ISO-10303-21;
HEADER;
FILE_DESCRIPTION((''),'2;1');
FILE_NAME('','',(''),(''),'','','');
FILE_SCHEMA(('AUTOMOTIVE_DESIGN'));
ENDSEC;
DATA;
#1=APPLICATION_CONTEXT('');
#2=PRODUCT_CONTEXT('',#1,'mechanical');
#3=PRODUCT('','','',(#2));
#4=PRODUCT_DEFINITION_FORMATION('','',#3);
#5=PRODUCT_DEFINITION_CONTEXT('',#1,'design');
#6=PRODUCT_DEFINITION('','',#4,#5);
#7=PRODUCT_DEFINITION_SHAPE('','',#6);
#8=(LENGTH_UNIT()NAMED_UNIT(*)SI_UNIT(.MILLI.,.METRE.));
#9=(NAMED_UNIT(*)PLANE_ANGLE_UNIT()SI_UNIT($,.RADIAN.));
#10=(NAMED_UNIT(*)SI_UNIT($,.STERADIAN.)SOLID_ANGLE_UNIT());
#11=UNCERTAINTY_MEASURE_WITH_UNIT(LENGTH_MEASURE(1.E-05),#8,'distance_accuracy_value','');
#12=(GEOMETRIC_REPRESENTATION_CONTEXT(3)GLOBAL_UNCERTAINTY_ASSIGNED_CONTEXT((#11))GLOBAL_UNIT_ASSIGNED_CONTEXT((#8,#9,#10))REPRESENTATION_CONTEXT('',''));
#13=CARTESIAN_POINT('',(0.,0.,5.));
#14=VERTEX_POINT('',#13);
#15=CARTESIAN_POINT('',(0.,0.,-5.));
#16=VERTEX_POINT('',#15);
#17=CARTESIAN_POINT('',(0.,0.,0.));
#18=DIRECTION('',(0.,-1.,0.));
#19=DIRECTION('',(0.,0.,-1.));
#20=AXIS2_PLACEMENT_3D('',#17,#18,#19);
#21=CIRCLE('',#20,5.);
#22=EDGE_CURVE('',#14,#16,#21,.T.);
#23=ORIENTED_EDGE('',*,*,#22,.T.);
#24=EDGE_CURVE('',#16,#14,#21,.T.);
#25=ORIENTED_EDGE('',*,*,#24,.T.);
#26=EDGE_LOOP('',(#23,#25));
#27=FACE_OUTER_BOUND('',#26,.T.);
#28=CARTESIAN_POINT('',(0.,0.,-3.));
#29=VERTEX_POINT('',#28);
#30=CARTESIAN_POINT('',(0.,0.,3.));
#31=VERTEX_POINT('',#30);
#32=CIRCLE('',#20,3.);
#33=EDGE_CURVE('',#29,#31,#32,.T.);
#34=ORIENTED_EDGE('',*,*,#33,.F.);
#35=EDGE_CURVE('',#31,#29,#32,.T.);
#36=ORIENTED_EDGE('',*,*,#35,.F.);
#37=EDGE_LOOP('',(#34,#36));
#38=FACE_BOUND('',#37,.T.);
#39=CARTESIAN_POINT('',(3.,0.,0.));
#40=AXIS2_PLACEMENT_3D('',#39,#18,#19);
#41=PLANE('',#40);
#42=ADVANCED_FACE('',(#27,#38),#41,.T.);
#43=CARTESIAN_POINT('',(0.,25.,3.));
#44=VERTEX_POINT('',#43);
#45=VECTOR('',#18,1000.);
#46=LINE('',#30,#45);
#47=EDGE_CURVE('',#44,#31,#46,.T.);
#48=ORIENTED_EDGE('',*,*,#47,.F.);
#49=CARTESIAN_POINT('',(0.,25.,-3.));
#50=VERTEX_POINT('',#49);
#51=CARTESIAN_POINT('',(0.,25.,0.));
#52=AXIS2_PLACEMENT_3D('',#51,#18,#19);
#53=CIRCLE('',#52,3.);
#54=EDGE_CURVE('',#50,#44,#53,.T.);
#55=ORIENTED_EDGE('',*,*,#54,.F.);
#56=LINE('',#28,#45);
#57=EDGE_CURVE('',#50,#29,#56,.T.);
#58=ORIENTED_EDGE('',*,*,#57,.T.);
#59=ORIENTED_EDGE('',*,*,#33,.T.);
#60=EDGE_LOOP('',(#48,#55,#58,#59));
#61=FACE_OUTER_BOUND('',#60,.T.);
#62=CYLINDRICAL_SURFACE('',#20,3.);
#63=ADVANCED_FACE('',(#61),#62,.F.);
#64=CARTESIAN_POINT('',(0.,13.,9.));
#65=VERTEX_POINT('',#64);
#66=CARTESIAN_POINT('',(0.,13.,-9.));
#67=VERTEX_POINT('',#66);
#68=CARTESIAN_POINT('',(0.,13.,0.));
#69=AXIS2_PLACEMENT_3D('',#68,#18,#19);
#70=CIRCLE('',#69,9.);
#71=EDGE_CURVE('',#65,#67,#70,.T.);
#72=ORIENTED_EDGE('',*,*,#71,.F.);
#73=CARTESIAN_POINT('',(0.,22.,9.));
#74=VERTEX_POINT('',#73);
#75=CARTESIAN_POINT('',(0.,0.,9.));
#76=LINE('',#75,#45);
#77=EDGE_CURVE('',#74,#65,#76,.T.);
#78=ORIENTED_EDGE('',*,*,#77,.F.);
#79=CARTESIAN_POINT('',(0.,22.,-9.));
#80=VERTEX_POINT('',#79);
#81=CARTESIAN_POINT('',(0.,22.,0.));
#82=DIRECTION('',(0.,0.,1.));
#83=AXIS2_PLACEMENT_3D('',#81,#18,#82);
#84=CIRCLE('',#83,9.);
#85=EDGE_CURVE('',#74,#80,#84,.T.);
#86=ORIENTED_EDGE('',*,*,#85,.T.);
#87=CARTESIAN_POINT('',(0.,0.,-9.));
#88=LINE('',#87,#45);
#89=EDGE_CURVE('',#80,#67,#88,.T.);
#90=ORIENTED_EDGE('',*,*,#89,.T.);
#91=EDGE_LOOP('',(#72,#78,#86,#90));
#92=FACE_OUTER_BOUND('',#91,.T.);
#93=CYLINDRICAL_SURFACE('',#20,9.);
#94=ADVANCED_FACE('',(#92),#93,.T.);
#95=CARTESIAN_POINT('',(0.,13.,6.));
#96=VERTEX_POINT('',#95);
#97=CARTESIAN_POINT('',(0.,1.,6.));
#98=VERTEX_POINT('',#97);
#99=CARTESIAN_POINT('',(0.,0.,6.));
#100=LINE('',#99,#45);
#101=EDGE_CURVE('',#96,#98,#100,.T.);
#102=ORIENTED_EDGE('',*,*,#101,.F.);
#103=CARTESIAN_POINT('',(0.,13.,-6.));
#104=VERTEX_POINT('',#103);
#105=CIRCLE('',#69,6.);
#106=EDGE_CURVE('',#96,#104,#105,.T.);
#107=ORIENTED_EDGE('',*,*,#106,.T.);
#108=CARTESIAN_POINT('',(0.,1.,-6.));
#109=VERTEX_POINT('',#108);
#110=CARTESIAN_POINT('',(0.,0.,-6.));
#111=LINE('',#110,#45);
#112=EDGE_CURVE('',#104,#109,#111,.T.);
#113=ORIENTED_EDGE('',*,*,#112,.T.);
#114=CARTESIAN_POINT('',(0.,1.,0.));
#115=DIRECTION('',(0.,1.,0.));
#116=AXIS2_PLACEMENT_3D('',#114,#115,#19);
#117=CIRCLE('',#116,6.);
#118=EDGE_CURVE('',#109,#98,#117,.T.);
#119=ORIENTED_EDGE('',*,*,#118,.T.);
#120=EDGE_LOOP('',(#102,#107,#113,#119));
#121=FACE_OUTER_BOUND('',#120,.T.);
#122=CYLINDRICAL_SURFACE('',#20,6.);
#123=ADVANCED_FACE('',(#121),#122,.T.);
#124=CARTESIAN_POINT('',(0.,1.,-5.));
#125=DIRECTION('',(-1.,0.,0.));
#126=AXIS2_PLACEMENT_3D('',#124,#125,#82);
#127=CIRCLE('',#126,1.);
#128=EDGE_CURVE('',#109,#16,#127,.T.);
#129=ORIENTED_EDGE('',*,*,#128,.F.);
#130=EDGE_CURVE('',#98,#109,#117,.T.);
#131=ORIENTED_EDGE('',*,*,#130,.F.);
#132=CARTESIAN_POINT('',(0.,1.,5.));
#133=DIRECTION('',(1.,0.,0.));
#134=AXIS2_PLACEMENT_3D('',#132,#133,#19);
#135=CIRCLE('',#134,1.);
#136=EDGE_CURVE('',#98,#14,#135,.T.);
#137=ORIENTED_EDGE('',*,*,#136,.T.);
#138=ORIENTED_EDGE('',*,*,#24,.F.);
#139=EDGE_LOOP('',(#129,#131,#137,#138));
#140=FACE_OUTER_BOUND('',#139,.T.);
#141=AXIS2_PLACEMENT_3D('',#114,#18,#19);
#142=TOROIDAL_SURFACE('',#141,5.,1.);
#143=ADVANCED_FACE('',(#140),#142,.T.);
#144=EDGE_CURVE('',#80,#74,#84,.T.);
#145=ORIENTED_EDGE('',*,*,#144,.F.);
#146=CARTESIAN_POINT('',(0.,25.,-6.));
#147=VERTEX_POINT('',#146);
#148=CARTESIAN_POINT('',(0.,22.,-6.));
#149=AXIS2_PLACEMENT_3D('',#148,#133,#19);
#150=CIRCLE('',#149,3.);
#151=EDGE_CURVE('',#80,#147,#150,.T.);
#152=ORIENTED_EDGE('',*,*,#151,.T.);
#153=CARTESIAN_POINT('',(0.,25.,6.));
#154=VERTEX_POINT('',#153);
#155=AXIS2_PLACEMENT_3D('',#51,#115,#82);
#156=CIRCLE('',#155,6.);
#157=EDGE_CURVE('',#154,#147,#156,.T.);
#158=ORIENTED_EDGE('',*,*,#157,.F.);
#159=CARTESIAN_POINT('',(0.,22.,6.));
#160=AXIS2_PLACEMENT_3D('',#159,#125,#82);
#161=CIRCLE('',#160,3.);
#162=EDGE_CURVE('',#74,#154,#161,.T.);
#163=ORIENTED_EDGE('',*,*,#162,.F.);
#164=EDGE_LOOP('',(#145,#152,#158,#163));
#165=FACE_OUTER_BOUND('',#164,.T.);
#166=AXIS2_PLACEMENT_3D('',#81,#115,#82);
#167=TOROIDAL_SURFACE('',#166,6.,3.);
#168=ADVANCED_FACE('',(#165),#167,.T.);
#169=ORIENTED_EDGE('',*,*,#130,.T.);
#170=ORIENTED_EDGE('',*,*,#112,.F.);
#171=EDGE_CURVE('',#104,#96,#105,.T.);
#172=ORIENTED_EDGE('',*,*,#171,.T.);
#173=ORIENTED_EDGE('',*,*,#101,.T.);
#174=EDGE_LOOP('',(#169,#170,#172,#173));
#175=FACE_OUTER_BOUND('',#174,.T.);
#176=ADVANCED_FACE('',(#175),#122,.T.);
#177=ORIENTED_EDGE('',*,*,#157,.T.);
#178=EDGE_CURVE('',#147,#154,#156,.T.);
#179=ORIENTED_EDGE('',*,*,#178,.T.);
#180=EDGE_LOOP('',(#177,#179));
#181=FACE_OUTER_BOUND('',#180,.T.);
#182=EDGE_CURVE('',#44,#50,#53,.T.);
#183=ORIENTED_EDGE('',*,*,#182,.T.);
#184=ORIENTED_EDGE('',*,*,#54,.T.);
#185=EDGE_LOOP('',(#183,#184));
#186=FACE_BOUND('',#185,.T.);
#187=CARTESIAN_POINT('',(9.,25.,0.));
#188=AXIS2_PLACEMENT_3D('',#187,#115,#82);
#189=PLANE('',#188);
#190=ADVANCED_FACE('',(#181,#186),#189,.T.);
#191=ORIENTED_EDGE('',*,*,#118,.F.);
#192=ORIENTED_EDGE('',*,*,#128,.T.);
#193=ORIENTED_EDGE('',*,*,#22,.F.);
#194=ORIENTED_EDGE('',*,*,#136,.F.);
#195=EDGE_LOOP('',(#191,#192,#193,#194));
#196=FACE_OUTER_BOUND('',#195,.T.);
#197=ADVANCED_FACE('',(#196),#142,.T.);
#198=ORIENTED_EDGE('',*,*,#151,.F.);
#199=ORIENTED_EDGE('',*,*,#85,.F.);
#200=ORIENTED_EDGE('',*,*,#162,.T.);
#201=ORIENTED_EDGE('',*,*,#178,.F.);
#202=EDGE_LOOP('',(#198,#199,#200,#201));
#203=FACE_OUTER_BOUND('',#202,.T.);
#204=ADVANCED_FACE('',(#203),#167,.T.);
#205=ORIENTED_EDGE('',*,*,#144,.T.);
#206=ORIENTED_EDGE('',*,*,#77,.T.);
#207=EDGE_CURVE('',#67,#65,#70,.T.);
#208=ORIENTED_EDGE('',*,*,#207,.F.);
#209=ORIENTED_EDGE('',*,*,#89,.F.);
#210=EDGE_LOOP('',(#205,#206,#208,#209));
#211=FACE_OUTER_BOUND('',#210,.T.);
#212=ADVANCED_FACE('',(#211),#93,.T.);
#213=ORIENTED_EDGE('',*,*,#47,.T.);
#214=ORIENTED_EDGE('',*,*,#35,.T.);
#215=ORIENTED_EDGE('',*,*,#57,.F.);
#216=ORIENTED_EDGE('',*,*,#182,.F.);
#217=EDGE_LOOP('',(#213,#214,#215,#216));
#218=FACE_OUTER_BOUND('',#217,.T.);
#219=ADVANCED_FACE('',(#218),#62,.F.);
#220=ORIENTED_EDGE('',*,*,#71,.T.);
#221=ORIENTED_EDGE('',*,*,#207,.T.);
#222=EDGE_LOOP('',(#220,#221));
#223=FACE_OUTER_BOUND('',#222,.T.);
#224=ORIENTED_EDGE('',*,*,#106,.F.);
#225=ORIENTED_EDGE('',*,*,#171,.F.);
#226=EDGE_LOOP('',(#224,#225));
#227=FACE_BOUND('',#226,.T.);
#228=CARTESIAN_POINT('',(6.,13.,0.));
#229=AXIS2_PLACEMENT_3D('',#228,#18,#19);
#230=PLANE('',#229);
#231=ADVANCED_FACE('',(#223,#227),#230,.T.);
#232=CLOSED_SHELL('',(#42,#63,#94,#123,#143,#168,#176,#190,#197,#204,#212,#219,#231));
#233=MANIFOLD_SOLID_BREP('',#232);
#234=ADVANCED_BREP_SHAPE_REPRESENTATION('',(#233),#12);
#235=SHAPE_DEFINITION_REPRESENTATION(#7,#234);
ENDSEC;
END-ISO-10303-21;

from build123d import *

# Parameters (mm, degrees)
FILLET_1_R = 3
FILLET_2_R = 1


with BuildPart() as part:
    # 草图1 → 旋转1 (revolve)
    with BuildSketch(Plane.XY, mode=Mode.PRIVATE) as revolve_1_sk:
        Polygon((3, 25), (3, 0), (6, 0), (6, 13), (9, 13), (9, 25), align=None)
    revolve(revolve_1_sk.sketch.rotate(Axis((0, 0, 0), (0, 1, 0)), 90), axis=Axis((0, 0, 0), (0, 1, 0)))

    # 圆角1
    fillet_1_edges = [part.edges().sort_by_distance(p)[0] for p in [
        (0, 25, 9),
    ]]
    fillet(fillet_1_edges, radius=FILLET_1_R)

    # 圆角2
    fillet_2_edges = [part.edges().sort_by_distance(p)[0] for p in [
        (0, 0, 6),
    ]]
    fillet(fillet_2_edges, radius=FILLET_2_R)


solid = part.part
